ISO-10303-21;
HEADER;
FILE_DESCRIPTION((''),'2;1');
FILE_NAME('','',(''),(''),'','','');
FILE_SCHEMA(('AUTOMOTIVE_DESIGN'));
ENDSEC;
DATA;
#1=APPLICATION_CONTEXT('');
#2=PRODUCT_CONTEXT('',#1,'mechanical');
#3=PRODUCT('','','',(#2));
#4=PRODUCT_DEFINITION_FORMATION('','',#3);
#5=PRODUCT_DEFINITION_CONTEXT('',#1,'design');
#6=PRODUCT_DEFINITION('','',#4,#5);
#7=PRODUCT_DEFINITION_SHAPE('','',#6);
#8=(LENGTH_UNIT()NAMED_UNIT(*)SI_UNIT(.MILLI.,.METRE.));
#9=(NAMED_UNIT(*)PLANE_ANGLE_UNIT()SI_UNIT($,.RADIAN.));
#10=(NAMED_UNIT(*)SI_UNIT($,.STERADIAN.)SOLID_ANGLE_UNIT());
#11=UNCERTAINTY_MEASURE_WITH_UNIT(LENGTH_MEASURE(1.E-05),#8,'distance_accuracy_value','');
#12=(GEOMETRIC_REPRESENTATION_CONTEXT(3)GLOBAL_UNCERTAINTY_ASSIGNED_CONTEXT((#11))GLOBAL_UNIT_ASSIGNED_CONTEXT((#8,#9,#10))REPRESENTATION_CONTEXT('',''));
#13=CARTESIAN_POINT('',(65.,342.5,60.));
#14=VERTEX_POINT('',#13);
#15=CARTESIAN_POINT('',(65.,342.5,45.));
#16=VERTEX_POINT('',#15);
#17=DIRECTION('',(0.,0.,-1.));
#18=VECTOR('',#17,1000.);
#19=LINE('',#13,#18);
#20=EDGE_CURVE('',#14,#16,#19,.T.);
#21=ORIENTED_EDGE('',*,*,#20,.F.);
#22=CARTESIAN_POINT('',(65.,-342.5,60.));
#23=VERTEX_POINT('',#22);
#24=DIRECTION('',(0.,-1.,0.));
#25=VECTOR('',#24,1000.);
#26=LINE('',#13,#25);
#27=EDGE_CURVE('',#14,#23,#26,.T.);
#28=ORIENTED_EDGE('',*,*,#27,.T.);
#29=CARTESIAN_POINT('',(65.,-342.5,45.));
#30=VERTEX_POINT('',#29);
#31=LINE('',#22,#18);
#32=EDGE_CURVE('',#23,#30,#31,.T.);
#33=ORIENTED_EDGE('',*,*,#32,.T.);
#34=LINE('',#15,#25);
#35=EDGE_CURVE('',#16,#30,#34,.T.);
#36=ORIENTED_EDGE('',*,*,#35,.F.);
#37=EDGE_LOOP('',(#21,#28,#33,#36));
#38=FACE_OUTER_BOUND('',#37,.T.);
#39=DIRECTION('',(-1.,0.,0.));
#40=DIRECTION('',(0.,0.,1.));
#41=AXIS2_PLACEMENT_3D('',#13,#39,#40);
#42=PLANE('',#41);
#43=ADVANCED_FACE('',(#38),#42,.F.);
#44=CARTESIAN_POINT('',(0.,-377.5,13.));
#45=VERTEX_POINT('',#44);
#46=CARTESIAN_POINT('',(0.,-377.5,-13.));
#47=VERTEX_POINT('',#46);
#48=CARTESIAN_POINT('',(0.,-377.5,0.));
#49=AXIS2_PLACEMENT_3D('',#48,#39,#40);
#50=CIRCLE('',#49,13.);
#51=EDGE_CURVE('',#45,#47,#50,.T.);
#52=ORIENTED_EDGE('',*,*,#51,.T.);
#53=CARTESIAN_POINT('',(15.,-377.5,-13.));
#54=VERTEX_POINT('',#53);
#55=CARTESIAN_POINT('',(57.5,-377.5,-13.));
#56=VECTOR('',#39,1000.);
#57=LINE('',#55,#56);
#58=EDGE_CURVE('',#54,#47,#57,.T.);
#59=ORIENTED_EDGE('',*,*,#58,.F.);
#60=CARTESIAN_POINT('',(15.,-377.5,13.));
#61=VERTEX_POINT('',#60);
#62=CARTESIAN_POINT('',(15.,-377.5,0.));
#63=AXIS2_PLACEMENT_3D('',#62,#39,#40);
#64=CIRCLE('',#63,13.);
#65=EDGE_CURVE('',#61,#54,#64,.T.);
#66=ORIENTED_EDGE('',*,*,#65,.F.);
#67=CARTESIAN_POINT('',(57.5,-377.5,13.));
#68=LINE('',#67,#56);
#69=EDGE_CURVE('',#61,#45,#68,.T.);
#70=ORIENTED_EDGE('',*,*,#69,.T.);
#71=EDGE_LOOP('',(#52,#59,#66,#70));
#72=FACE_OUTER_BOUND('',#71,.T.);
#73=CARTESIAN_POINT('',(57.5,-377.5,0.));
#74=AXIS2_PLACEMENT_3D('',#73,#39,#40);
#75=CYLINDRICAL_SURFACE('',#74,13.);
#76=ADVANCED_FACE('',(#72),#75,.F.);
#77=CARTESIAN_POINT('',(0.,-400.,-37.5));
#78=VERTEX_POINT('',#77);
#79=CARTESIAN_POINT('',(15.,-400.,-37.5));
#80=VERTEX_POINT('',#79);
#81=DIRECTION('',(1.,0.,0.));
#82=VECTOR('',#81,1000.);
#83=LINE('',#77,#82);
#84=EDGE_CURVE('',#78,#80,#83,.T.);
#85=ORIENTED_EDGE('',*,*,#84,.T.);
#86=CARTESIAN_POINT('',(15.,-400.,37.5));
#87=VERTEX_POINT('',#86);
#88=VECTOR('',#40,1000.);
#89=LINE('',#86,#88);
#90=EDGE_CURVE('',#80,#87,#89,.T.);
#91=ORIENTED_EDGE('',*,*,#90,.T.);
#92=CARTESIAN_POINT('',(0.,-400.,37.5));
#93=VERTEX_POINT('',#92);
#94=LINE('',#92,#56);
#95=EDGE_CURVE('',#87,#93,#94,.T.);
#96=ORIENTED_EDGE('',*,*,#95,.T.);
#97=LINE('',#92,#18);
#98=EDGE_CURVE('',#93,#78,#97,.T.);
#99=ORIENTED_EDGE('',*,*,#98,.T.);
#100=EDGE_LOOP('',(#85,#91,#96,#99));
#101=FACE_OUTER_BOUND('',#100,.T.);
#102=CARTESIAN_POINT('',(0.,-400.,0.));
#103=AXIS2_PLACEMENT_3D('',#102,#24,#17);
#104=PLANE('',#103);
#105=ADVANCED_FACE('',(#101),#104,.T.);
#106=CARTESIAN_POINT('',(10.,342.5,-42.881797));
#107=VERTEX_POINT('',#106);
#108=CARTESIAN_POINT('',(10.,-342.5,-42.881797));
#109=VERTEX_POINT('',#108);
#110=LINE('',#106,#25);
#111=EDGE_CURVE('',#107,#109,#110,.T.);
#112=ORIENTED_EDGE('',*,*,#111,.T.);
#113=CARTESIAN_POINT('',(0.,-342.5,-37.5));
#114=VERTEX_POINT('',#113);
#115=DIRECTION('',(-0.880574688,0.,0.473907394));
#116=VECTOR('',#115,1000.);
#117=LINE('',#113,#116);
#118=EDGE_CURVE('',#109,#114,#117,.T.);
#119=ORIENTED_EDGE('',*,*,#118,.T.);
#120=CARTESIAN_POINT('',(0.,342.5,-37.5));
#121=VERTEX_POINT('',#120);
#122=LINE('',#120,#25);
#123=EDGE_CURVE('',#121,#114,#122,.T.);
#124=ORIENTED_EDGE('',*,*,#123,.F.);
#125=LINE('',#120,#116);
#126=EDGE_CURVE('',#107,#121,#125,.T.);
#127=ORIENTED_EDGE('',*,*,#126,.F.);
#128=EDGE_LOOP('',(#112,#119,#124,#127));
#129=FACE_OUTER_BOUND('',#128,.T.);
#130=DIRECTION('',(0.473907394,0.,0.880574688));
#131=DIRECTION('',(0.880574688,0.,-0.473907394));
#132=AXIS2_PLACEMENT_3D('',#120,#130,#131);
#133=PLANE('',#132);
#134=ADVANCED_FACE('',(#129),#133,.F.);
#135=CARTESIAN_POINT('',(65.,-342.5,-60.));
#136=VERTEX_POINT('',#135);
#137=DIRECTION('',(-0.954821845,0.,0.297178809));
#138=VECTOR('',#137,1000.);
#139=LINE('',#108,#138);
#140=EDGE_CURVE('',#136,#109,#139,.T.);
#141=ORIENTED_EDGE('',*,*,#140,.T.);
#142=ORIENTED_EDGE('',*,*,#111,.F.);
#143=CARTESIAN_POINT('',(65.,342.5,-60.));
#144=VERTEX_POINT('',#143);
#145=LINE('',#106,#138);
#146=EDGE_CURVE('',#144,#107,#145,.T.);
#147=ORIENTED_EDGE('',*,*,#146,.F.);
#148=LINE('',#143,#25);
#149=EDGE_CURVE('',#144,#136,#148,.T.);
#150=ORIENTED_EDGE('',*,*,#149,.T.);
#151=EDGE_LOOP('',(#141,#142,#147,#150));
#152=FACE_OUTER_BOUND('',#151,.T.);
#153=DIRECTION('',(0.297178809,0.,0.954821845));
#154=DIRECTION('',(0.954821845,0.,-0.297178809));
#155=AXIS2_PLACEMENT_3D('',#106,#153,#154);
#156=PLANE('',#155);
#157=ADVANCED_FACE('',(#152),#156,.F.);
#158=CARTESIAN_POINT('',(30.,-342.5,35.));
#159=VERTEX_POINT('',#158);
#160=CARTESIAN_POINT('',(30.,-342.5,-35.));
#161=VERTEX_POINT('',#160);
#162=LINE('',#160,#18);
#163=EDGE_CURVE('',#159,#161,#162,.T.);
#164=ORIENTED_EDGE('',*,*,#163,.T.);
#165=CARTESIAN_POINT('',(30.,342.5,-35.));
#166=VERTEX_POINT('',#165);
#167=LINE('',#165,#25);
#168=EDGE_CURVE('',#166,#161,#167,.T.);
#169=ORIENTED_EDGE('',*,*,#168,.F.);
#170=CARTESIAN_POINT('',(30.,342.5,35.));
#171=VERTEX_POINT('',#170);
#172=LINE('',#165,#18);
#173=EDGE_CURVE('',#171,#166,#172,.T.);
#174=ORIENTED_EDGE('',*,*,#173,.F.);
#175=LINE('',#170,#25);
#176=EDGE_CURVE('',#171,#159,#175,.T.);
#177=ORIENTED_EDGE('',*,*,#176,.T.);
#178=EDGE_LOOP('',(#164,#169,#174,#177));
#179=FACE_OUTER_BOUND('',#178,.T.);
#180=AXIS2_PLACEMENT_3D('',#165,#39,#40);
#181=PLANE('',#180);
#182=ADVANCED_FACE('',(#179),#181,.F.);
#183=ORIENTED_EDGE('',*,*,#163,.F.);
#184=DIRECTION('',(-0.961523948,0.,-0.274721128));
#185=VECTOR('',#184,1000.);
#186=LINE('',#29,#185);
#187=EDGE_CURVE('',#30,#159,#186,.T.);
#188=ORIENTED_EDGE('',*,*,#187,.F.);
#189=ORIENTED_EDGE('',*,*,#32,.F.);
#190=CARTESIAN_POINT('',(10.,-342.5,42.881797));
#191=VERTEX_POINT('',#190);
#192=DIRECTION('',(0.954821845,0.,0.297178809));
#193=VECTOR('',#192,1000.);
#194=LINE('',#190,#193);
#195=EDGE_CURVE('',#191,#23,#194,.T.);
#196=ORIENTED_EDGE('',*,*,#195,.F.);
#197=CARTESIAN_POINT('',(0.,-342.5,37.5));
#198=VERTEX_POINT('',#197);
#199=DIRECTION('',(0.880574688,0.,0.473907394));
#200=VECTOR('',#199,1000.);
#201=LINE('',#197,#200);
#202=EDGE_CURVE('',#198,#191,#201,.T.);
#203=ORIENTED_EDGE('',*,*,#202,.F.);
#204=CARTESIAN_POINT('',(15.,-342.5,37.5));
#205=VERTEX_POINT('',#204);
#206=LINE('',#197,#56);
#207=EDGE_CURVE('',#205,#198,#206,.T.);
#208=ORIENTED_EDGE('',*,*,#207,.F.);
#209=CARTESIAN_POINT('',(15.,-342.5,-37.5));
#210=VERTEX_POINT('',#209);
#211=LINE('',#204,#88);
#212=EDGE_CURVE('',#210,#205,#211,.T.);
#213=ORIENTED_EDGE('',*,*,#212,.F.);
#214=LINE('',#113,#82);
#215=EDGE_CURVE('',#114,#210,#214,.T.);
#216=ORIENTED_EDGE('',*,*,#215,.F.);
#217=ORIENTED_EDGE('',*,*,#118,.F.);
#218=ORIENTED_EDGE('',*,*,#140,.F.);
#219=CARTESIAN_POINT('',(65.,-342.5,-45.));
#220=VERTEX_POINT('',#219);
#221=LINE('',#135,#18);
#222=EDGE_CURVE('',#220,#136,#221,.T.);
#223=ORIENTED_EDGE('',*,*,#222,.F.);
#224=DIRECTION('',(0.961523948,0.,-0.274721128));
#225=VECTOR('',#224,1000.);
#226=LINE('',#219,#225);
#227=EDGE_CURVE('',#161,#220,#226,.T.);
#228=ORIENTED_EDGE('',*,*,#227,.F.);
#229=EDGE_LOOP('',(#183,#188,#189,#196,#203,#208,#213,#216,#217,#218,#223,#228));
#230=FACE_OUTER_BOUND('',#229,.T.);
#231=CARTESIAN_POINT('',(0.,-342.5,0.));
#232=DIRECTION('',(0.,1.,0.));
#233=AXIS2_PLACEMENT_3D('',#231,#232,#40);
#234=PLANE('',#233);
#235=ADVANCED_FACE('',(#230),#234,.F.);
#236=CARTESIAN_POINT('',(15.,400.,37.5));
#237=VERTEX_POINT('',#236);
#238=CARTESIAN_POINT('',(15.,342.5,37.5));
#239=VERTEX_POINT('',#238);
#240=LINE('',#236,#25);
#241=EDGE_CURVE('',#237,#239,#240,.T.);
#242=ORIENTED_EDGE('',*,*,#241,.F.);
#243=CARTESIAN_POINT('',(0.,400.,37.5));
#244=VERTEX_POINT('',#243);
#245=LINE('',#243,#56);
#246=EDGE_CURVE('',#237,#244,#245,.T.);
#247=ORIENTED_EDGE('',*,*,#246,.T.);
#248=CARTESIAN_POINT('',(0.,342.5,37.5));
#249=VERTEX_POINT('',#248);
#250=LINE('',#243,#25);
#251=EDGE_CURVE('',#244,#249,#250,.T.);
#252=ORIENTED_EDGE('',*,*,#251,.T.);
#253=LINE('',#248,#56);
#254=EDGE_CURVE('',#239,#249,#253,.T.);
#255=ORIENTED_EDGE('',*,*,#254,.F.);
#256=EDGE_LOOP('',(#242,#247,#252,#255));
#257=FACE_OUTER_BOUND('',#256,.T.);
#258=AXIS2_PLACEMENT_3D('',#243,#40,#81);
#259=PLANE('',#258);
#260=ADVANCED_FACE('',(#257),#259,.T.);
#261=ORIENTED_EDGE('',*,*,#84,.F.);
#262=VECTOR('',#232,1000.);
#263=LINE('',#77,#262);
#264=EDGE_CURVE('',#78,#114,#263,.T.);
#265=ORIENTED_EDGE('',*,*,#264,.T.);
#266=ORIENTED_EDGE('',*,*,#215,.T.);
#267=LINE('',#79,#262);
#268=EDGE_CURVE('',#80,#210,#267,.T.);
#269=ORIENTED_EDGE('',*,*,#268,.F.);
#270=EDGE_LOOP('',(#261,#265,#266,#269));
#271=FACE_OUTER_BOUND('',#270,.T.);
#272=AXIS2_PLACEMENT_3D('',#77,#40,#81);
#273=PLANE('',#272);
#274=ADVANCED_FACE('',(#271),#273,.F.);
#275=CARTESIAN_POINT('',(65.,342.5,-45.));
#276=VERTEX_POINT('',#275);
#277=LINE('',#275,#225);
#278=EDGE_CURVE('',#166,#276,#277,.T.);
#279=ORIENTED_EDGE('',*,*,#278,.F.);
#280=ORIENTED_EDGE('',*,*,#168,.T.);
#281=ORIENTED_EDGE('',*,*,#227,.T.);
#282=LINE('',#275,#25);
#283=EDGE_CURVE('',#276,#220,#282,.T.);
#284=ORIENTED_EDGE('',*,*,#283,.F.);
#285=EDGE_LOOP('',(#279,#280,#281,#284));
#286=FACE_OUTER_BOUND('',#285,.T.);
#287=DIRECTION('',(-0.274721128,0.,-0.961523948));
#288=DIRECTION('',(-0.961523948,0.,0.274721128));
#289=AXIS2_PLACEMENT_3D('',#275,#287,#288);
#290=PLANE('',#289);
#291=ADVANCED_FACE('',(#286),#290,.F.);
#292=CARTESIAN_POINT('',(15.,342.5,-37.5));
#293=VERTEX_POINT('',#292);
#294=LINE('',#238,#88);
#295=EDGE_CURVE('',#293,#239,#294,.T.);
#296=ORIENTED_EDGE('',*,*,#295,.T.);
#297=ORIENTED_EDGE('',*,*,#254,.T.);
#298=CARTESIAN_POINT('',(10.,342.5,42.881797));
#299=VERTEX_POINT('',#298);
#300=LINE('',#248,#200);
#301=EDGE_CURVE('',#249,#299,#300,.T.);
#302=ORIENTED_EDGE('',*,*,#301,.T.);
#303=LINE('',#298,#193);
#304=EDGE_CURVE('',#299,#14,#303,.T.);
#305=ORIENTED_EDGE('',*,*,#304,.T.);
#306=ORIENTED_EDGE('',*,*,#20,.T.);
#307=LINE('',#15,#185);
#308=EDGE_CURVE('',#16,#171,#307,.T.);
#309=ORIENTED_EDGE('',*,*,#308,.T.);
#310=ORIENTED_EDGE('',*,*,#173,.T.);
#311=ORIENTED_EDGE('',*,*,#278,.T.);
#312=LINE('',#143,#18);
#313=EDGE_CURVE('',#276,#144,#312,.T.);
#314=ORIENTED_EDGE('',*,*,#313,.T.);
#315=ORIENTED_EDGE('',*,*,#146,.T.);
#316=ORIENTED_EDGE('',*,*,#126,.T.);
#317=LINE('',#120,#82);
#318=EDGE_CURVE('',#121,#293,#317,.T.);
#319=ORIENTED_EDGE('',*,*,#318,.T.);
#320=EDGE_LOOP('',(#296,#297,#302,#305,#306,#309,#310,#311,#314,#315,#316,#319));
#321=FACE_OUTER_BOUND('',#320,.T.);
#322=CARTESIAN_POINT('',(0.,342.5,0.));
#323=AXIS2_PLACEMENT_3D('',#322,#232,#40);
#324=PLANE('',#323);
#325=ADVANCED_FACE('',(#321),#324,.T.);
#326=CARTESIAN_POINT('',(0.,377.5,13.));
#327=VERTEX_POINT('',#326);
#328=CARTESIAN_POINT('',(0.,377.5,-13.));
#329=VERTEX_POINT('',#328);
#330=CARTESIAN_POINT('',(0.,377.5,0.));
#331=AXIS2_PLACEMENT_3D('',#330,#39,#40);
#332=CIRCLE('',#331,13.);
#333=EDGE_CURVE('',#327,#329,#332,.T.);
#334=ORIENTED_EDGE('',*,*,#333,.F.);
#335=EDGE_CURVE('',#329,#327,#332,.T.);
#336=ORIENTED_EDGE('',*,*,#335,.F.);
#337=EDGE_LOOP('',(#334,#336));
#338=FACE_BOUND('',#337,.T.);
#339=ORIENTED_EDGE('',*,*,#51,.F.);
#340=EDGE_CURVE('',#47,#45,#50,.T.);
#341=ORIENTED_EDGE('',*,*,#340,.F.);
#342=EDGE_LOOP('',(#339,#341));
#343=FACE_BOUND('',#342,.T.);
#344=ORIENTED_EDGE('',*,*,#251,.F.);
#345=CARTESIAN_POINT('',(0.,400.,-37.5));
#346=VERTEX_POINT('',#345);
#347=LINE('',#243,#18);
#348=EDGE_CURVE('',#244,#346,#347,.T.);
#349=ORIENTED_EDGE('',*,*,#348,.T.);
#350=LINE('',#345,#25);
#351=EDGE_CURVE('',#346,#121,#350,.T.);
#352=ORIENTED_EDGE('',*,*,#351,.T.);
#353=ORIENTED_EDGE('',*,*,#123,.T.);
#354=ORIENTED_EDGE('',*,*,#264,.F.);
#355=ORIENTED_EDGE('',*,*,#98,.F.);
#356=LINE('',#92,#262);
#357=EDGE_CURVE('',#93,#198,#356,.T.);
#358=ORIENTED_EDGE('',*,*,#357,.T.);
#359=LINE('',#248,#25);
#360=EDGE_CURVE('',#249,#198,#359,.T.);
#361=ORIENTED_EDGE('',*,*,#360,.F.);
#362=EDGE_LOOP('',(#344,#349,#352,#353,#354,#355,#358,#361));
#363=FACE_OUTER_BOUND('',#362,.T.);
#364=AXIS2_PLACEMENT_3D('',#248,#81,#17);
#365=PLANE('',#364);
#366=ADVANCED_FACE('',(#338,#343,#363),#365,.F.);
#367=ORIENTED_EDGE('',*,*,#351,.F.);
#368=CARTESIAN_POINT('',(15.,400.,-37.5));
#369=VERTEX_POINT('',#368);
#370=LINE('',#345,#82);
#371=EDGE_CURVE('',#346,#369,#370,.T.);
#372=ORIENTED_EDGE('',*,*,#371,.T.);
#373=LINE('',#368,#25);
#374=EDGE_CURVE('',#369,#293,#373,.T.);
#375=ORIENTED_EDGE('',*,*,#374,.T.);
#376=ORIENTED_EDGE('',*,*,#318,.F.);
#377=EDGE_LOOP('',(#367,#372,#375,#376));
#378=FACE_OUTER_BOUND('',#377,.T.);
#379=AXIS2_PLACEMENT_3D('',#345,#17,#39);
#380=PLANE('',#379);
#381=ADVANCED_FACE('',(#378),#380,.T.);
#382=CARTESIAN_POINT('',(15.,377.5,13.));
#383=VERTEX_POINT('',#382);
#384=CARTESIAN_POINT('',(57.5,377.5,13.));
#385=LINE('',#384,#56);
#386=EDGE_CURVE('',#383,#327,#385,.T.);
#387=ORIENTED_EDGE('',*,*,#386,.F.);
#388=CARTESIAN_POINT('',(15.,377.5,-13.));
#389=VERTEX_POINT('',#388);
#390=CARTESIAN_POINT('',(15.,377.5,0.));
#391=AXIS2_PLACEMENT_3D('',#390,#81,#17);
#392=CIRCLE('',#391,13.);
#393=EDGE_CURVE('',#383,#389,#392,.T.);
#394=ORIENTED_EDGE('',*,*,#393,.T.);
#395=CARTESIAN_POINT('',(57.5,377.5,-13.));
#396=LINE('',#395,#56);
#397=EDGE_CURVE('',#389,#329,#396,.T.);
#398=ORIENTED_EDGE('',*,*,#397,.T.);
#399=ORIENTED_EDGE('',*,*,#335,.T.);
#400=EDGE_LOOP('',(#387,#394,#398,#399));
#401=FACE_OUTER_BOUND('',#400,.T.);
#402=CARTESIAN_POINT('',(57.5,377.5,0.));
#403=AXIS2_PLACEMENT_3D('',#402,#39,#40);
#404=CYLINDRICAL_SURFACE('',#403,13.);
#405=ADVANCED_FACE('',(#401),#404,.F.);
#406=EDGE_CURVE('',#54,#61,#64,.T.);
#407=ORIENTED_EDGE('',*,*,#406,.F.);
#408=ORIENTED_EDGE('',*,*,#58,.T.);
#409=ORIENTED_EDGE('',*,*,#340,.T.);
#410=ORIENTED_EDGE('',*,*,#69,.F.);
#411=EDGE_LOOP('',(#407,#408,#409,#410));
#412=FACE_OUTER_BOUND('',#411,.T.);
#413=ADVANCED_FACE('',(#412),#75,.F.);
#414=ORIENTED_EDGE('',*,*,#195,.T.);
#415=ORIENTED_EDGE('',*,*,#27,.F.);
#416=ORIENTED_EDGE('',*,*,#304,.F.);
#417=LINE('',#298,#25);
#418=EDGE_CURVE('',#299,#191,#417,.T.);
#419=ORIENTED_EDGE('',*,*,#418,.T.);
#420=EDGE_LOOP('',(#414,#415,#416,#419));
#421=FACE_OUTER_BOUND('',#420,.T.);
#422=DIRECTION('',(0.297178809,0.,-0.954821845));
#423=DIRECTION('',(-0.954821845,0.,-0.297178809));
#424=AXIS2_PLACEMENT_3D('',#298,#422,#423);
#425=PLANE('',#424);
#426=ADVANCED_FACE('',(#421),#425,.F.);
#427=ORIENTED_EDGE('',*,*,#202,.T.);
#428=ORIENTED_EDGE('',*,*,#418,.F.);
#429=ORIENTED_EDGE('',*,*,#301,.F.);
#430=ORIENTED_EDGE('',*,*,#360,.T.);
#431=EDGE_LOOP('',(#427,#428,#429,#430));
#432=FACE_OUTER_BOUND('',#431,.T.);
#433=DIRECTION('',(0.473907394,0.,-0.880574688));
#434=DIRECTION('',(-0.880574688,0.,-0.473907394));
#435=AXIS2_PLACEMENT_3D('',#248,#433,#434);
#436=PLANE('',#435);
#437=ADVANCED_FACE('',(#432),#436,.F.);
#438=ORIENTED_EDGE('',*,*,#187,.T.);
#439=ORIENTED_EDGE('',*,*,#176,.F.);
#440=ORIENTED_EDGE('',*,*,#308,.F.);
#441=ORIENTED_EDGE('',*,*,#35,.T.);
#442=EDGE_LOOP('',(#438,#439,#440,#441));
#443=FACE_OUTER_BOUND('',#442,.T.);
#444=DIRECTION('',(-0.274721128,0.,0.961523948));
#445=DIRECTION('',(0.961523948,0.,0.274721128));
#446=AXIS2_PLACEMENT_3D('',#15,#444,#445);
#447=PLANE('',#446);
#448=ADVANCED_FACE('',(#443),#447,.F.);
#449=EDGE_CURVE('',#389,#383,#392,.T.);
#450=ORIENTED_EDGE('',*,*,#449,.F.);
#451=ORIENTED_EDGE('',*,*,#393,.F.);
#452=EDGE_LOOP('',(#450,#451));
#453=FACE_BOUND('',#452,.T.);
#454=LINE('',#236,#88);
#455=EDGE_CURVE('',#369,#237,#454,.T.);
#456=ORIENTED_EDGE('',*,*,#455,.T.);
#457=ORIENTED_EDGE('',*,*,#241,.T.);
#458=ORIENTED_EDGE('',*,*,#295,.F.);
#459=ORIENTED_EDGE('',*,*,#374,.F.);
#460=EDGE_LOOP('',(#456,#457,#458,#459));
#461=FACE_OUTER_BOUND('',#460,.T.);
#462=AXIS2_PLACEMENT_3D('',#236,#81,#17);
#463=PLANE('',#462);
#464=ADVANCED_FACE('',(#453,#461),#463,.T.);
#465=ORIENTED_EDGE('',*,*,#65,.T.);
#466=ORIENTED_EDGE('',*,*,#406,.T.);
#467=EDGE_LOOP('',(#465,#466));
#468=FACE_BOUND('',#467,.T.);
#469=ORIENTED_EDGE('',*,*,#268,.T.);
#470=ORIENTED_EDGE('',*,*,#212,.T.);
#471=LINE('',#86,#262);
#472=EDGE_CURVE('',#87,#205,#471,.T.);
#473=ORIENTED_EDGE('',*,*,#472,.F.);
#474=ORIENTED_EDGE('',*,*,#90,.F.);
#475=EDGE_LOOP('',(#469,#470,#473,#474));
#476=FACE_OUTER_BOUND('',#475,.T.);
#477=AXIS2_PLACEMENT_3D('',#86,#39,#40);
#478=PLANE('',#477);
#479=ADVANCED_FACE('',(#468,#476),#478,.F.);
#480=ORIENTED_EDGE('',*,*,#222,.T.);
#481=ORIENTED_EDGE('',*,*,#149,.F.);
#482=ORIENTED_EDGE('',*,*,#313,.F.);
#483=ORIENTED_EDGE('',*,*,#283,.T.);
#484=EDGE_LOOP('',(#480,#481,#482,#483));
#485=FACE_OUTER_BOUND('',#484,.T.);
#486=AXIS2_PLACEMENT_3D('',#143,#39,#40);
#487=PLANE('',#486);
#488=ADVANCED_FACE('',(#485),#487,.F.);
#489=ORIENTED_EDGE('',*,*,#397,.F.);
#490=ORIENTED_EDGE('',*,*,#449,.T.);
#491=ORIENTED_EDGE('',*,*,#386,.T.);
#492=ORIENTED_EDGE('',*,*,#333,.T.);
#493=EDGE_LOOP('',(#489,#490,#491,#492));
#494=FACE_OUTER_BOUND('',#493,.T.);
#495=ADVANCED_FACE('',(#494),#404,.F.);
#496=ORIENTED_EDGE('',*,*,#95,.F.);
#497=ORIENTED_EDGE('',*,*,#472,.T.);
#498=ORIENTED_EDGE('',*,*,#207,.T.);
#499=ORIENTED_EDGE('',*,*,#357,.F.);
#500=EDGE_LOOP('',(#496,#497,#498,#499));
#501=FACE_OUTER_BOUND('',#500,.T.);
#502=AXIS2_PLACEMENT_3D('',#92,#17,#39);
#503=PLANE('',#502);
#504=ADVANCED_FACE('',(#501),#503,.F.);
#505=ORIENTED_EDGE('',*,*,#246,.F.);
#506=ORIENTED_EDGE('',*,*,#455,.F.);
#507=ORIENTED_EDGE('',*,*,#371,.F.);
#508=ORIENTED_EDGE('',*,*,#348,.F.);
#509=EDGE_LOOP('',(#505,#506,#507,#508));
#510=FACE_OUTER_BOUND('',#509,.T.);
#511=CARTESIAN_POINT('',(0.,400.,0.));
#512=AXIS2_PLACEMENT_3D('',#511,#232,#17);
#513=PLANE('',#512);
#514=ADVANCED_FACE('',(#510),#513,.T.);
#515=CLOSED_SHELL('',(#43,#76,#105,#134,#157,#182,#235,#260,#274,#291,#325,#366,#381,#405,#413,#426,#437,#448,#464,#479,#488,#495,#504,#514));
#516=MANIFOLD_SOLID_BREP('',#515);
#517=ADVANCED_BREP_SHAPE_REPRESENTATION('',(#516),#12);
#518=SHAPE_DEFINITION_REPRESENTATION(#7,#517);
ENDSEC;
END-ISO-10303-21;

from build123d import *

# Parameters (mm, degrees)
BOSS_EXTRUDE1_DEPTH = 342.5
SKETCH2_W           = 15
SKETCH2_H           = 75
BOSS_EXTRUDE2_DEPTH = 57.5
SKETCH3_R           = 13
CUT_EXTRUDE1_DEPTH  = 57.5


with BuildPart() as part:
    # Sketch1 → Boss-Extrude1 (new, symmetric)
    with BuildSketch(Plane(origin=(0, 0, 0), x_dir=(1, 0, 0), z_dir=(0, 1, 0))):
        Polygon((0, -37.5), (0, 37.5), (10, 42.881796684), (65, 60), (65, 45), (30, 35), (30, -35), (65, -45), (65, -60), (10, -42.881796684), align=None)
    extrude(amount=BOSS_EXTRUDE1_DEPTH, both=True)

    # Sketch2 → Boss-Extrude2 (add)
    with BuildSketch(Plane.XZ.offset(342.5)):
        with Locations((7.5, 0)):
            Rectangle(SKETCH2_W, SKETCH2_H)
    boss_extrude2 = extrude(amount=BOSS_EXTRUDE2_DEPTH)

    # Mirror1: Boss-Extrude2 across plane
    add(boss_extrude2.mirror(Plane.ZX))

    # Sketch3 → Cut-Extrude1 (cut)
    with BuildSketch(Plane.ZY):
        with Locations((0, 377.5)):
            Circle(SKETCH3_R)
        with Locations((0, -377.5)):
            Circle(SKETCH3_R)
    extrude(amount=-CUT_EXTRUDE1_DEPTH, mode=Mode.SUBTRACT)


solid = part.part
